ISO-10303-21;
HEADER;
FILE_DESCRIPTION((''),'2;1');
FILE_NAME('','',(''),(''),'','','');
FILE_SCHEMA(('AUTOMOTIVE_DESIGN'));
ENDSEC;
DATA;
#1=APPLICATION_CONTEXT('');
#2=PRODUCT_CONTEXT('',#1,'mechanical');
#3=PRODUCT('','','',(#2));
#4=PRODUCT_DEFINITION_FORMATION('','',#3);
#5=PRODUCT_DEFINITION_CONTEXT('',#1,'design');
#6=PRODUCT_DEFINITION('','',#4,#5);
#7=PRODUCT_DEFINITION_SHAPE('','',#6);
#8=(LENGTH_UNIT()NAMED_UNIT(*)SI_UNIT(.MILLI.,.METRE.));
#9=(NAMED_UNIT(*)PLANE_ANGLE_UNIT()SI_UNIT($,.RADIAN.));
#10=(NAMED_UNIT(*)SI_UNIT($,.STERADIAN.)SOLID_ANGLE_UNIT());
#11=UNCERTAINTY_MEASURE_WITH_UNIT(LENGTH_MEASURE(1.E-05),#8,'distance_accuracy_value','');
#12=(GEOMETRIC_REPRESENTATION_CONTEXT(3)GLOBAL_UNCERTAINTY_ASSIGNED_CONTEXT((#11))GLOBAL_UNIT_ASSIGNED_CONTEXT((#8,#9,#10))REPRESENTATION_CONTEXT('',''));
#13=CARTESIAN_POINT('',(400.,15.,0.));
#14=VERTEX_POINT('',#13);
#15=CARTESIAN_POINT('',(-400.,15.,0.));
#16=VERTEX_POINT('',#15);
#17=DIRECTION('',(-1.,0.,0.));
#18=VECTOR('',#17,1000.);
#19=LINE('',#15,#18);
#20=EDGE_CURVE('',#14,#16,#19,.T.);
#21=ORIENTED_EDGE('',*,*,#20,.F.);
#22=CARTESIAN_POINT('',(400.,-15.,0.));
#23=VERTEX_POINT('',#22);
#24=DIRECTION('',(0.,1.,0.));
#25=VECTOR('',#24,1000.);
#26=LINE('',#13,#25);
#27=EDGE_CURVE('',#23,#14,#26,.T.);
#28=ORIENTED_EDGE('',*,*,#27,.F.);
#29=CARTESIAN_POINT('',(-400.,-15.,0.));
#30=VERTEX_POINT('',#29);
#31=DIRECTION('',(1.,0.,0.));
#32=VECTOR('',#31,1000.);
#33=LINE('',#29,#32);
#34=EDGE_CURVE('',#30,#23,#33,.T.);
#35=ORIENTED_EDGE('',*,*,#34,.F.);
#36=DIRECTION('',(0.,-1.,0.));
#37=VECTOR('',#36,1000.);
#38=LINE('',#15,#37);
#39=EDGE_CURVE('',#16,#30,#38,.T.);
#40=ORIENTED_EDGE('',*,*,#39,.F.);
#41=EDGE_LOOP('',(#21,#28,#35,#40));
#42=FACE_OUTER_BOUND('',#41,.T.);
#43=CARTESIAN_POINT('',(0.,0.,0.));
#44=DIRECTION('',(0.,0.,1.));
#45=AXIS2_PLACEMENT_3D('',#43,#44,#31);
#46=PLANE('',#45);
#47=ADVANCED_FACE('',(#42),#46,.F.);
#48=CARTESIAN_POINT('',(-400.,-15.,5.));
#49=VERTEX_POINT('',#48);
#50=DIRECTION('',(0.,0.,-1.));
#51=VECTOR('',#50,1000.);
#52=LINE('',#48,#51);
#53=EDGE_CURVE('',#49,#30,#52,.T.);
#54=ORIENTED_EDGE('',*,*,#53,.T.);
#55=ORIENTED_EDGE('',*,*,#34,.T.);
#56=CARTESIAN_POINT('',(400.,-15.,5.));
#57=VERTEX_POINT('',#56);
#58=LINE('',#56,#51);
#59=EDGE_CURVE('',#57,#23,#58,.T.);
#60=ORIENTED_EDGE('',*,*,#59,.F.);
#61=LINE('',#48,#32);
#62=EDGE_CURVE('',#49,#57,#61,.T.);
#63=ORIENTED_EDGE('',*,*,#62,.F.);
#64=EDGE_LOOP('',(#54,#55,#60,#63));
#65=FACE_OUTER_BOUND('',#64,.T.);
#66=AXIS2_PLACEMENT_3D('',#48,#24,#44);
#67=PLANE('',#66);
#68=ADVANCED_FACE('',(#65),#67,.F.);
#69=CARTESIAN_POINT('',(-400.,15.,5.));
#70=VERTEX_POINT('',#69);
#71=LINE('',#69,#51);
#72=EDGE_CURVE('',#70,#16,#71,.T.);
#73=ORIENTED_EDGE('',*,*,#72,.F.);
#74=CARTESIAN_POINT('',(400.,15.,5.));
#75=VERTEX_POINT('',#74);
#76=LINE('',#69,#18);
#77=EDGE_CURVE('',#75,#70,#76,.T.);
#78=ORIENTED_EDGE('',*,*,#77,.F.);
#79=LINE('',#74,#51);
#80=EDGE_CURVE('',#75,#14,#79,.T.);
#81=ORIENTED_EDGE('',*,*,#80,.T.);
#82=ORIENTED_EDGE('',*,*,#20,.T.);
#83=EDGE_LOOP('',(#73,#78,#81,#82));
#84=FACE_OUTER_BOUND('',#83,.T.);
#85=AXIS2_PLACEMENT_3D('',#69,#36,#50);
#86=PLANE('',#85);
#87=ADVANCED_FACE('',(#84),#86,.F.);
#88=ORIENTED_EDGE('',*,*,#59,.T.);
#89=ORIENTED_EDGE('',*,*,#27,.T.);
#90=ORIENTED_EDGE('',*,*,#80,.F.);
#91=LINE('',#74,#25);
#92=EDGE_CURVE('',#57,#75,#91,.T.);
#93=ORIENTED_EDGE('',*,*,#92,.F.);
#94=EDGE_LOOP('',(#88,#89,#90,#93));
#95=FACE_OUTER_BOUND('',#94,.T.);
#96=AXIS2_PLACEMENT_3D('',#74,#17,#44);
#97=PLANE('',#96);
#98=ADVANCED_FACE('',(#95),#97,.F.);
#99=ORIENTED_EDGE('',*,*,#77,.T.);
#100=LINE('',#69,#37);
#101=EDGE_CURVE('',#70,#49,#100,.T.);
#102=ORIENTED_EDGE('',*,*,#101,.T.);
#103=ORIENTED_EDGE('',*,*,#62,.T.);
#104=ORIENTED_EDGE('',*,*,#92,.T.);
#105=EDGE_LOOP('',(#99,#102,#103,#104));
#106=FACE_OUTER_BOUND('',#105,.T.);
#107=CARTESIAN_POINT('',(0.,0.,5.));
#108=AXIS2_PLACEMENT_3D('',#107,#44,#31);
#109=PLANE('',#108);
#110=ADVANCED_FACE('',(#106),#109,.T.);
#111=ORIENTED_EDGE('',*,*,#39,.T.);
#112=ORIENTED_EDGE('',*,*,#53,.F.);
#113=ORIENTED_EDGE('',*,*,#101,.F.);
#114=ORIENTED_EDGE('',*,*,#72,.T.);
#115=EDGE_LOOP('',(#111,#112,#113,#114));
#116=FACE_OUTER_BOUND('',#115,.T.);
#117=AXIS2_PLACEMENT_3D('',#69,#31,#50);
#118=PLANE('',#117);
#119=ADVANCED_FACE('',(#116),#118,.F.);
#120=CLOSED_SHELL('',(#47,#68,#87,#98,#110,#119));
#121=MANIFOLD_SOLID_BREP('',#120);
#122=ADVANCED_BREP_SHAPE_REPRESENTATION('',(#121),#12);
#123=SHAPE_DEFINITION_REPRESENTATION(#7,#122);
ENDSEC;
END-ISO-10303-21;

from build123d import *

# Parameters (mm, degrees)
SKETCH1_W           = 800
SKETCH1_H           = 30
BOSS_EXTRUDE1_DEPTH = 5


with BuildPart() as part:
    # Sketch1 → Boss-Extrude1 (new body)
    with BuildSketch(Plane.XY):
        Rectangle(SKETCH1_W, SKETCH1_H)
    extrude(amount=BOSS_EXTRUDE1_DEPTH)


solid = part.part
